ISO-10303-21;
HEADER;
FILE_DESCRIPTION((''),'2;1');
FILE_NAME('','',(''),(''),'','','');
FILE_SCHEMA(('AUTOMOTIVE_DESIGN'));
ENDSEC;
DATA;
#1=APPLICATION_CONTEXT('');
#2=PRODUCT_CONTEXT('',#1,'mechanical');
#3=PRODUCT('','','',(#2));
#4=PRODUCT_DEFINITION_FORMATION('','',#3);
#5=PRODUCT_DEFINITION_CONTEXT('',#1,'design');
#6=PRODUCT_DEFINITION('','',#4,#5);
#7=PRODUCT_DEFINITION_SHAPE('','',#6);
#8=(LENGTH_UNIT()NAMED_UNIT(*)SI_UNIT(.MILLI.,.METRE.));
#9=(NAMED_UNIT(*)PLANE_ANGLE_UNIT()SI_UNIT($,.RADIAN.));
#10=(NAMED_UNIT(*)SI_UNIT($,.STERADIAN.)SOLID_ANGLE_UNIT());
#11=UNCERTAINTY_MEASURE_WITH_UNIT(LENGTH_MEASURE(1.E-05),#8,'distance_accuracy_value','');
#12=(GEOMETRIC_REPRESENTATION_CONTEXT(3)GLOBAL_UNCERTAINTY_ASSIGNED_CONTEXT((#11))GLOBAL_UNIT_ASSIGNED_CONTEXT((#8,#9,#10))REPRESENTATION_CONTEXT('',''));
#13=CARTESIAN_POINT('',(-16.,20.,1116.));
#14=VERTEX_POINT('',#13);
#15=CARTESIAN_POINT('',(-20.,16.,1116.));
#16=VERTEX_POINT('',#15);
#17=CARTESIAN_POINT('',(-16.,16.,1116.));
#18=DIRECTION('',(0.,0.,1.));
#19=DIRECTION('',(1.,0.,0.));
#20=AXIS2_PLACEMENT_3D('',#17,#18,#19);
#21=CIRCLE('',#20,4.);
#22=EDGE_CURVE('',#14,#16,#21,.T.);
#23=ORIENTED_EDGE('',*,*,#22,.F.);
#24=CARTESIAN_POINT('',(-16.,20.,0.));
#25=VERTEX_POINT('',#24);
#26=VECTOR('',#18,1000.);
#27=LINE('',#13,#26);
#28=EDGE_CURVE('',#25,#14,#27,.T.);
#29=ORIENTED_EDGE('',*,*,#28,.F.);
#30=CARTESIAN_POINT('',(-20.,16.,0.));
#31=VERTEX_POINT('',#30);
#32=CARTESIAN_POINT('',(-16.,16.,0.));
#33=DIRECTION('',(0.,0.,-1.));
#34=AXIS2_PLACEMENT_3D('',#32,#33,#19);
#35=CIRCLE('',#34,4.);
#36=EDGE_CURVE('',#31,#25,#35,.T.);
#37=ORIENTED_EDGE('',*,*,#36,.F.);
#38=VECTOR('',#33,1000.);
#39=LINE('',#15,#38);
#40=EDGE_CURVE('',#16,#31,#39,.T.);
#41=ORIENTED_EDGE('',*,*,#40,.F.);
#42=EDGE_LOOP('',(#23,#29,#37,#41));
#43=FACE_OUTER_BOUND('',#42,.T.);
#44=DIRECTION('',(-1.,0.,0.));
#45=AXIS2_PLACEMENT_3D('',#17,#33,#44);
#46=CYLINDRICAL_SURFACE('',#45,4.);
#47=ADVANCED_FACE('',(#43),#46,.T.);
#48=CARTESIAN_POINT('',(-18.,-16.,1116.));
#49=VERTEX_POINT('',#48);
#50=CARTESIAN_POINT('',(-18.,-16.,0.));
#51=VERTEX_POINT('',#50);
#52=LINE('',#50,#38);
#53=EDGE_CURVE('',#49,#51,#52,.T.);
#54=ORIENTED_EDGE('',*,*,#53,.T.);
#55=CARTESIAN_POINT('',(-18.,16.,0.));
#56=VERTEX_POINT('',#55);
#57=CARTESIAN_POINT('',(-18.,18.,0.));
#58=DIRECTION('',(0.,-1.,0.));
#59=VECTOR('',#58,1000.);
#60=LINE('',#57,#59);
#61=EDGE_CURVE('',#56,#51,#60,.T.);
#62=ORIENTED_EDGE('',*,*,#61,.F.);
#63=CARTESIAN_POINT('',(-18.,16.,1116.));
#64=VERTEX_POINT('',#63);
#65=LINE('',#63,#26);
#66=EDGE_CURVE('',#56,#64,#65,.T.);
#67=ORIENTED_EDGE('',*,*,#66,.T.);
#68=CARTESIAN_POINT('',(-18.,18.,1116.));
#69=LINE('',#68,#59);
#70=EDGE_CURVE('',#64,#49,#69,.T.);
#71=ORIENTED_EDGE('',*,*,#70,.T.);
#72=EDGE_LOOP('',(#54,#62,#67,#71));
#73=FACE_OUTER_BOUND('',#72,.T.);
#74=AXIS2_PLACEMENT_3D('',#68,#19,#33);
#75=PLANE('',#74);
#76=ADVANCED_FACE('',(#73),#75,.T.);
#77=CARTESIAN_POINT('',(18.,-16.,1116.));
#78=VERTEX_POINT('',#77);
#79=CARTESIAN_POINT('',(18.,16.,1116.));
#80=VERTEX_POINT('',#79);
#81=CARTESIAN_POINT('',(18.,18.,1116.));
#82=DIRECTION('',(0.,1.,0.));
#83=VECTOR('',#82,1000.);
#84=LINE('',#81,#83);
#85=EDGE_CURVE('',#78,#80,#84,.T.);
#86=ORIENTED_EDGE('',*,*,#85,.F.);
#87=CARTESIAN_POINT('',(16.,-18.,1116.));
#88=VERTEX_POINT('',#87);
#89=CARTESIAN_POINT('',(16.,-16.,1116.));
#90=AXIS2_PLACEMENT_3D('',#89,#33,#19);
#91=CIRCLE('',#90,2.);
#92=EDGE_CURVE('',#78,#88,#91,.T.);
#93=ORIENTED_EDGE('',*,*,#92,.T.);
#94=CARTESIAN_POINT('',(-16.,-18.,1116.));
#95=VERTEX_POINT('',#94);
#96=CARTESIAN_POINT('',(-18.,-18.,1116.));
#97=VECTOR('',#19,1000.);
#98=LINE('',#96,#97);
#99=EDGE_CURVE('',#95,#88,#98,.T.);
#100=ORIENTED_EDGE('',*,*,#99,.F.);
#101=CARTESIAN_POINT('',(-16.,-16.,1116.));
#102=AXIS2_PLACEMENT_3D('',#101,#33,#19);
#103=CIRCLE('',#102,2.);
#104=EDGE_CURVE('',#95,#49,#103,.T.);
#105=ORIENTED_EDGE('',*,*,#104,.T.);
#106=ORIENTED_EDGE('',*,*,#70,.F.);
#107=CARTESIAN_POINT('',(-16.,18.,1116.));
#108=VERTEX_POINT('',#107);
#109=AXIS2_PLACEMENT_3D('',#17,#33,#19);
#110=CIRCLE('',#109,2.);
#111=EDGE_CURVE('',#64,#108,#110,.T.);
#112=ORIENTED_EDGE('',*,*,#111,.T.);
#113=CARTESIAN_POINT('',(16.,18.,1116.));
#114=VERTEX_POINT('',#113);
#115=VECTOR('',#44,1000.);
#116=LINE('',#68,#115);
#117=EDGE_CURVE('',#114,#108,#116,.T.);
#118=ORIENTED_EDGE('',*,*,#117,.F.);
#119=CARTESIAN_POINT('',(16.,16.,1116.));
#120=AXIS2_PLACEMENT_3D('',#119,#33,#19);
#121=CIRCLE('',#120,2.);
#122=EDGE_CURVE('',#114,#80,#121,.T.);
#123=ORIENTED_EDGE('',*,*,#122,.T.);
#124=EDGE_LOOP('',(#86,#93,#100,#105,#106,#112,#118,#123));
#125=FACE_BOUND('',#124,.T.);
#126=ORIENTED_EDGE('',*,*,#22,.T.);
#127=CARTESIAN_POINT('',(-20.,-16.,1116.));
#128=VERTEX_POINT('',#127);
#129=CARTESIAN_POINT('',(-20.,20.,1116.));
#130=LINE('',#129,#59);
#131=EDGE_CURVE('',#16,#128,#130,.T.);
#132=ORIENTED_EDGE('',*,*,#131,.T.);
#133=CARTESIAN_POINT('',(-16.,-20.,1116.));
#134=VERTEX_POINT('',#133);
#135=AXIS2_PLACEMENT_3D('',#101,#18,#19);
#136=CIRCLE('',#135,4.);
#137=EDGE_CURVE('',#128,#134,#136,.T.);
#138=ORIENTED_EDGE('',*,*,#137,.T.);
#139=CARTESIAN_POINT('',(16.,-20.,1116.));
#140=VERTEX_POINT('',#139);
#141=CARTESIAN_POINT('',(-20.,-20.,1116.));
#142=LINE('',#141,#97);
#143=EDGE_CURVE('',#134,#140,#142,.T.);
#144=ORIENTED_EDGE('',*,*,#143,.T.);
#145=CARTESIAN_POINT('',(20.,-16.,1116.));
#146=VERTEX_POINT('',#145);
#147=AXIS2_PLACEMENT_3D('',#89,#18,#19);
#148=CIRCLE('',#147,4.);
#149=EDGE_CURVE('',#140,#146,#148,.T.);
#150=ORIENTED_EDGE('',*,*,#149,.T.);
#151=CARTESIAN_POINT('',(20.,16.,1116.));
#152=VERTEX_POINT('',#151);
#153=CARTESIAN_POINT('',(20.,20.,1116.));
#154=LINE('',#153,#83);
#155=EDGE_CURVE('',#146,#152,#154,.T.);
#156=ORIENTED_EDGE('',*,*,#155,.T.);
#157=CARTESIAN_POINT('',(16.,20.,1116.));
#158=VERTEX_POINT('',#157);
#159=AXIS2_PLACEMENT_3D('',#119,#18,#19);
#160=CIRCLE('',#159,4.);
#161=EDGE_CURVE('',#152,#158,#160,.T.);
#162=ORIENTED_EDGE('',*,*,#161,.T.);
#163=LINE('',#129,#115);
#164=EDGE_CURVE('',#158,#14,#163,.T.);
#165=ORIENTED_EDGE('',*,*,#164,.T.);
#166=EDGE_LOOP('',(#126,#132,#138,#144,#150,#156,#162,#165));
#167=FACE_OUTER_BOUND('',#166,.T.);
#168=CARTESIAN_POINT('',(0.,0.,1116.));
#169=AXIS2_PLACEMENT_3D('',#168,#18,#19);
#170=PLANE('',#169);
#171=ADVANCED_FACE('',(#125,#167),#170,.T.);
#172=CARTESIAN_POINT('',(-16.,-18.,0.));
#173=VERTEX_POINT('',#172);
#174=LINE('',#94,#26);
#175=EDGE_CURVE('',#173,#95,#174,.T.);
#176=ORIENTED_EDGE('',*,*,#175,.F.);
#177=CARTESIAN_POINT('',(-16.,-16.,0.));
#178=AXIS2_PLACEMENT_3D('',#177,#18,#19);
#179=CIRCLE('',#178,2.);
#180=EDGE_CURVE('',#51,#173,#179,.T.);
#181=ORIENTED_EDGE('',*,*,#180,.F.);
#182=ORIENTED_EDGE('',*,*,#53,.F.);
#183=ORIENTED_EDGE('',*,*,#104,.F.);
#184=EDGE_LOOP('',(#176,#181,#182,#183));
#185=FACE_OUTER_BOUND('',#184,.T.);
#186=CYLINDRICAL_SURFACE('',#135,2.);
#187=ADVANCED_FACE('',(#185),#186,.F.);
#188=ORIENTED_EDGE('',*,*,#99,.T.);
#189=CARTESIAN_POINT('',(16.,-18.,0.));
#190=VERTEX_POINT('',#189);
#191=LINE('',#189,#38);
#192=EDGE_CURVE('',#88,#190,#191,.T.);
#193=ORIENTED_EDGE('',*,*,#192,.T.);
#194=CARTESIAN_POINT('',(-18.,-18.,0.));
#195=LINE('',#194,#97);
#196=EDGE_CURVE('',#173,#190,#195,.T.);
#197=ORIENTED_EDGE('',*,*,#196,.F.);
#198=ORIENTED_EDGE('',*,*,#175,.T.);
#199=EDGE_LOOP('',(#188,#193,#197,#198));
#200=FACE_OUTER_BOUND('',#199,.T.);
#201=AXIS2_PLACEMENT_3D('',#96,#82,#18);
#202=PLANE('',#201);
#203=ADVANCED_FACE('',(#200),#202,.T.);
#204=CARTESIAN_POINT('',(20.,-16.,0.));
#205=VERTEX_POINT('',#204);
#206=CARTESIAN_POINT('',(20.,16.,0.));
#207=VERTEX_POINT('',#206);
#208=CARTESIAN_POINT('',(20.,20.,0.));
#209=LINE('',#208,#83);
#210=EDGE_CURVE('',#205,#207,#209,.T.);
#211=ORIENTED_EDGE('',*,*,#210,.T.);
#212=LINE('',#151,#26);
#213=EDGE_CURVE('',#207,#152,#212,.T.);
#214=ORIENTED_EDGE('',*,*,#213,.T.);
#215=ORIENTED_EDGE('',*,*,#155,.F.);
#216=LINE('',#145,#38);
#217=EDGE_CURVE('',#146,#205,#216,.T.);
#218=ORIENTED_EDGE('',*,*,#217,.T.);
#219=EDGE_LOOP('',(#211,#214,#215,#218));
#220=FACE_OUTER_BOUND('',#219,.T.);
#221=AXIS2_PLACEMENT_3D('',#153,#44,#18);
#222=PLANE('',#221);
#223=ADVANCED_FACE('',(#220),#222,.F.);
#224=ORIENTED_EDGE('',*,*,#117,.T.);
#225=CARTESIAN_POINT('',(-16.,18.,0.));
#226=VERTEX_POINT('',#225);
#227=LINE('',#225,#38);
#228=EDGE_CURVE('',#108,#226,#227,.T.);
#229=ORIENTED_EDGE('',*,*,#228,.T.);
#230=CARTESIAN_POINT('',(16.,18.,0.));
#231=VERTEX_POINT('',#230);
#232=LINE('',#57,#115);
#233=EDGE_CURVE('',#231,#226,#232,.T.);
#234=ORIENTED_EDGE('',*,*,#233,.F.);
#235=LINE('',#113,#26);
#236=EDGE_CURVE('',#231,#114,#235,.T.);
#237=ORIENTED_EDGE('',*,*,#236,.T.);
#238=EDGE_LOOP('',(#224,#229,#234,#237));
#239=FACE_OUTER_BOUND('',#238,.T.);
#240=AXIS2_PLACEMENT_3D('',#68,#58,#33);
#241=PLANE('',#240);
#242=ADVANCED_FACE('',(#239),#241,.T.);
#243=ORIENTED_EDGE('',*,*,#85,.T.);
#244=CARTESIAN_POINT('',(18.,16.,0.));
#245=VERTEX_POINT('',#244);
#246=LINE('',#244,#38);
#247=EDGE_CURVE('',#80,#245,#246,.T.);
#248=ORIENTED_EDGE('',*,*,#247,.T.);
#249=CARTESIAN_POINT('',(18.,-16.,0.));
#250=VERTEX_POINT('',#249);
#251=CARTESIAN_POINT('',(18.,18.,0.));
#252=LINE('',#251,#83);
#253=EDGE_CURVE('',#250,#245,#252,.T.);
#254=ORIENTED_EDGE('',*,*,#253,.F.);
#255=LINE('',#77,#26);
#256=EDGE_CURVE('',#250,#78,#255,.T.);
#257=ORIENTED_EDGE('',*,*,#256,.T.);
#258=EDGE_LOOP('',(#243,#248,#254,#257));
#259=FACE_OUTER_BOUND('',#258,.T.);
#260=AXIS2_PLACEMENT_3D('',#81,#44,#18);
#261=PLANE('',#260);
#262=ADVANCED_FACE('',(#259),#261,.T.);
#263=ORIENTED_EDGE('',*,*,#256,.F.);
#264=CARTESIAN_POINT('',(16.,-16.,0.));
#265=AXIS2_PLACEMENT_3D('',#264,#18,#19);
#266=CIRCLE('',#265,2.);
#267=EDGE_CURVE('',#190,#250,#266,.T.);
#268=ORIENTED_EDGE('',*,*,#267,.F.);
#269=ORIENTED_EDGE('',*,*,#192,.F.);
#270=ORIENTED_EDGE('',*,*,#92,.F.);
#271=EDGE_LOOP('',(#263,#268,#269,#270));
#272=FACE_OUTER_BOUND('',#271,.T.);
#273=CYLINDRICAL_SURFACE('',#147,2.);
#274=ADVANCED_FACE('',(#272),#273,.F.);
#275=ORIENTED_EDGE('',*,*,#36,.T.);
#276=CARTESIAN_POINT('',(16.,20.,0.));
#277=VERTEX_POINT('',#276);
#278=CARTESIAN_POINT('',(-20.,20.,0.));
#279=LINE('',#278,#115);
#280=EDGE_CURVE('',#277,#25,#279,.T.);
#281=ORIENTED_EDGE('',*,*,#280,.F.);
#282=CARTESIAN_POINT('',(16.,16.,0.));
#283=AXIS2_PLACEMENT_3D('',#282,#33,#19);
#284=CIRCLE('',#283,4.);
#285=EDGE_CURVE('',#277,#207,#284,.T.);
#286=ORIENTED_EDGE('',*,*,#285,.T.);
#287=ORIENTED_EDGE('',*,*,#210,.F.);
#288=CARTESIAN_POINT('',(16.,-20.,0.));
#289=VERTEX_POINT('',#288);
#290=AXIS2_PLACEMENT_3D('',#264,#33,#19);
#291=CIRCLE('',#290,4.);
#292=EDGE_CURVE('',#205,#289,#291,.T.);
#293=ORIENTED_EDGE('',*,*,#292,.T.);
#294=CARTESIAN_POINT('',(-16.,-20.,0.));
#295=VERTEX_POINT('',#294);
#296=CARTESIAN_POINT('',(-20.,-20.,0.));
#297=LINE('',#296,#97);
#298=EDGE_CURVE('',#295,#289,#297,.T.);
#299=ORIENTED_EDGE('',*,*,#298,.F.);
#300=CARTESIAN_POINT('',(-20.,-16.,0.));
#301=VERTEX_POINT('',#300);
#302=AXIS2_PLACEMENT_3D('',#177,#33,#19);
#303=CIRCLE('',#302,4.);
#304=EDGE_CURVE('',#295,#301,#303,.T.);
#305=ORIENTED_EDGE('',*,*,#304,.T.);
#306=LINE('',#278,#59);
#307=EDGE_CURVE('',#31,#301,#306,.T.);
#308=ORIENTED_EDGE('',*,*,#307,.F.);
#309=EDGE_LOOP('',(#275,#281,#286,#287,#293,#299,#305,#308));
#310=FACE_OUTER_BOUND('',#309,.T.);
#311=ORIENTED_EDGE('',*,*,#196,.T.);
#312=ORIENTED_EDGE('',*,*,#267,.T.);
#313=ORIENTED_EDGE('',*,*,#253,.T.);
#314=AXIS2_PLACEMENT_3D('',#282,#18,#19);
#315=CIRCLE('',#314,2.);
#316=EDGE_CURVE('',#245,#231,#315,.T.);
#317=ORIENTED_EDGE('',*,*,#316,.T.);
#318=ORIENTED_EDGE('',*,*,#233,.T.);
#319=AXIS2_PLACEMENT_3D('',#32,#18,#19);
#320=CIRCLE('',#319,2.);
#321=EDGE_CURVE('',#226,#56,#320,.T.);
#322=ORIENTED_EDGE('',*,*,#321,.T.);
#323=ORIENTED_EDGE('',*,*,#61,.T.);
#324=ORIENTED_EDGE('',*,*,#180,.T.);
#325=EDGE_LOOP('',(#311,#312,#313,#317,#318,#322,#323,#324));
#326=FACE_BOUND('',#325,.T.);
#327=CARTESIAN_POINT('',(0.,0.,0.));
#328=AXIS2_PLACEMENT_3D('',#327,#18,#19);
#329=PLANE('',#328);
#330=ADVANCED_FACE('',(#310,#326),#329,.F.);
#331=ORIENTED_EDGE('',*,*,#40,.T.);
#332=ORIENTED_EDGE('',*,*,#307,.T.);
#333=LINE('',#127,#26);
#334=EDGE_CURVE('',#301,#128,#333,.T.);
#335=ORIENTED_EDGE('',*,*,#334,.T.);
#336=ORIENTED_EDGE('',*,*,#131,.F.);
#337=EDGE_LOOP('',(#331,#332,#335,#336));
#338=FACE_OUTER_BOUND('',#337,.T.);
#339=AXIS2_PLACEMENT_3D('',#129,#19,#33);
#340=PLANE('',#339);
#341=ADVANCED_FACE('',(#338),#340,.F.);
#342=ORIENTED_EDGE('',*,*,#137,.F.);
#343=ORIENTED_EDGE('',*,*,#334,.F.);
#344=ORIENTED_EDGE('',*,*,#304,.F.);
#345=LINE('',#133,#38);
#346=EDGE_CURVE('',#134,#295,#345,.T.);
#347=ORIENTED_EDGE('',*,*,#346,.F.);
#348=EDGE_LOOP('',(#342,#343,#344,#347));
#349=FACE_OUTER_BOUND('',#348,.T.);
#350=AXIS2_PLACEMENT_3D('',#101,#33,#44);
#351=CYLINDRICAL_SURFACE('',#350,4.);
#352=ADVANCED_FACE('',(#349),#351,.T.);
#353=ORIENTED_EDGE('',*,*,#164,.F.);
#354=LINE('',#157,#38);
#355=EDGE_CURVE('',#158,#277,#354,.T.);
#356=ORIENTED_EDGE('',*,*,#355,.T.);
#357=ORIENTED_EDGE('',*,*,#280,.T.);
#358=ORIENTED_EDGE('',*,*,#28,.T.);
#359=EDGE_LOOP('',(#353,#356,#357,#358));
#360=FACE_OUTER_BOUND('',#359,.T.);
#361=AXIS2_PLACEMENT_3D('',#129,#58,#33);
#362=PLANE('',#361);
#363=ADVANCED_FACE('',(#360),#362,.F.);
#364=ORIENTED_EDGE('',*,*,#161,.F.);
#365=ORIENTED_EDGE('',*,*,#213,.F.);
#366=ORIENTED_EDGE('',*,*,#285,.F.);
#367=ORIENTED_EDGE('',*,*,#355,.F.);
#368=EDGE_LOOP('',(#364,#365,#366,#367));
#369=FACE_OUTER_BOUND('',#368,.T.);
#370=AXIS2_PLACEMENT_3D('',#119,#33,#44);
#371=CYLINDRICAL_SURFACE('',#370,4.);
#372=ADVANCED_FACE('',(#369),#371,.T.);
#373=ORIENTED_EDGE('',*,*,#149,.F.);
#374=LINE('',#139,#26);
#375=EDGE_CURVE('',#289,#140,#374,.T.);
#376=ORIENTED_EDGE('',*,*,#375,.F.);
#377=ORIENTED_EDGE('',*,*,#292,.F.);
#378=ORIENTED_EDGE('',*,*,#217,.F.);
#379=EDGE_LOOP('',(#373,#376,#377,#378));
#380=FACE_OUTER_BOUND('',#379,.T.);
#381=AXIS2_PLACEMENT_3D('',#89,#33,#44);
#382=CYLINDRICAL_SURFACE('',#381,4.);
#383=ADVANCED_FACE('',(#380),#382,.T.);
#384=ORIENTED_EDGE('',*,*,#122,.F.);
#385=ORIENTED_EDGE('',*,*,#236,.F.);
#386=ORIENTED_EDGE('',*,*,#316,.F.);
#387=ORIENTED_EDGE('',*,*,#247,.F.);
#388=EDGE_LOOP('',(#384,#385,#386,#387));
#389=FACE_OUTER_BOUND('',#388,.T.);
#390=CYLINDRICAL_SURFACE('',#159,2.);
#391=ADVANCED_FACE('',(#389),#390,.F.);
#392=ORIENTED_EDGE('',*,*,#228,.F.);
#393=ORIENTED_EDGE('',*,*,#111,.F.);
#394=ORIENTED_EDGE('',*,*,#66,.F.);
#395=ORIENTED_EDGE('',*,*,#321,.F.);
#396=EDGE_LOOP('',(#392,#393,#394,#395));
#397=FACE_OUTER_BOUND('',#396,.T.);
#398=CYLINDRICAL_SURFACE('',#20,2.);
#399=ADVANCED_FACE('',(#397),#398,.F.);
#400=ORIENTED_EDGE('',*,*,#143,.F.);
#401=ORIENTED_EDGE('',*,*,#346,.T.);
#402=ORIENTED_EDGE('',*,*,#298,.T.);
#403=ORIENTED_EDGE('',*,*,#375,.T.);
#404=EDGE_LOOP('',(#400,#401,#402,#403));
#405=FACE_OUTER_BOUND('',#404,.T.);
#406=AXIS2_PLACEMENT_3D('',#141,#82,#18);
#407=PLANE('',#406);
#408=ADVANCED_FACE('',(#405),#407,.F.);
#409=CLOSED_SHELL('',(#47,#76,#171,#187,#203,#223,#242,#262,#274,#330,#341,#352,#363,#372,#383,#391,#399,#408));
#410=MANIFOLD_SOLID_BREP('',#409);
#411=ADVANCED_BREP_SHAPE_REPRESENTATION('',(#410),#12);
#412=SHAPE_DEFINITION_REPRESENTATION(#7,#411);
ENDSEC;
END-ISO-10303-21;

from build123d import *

# Parameters (mm, degrees)
SKETCH1_W           = 40
SKETCH1_H           = 40
SKETCH1_W_2         = 36
SKETCH1_H_2         = 36
BOSS_EXTRUDE1_DEPTH = 1116
FILLET1_R           = 2
FILLET2_R           = 4


with BuildPart() as part:
    # Sketch1 → Boss-Extrude1 (new body)
    with BuildSketch(Plane.XY):
        Rectangle(SKETCH1_W, SKETCH1_H)
        Rectangle(SKETCH1_W_2, SKETCH1_H_2, mode=Mode.SUBTRACT)
    extrude(amount=BOSS_EXTRUDE1_DEPTH)

    # Fillet1
    fillet1_edges = [part.edges().sort_by_distance(p)[0] for p in [
        (18, -18, 558),
        (18, 18, 558),
        (-18, 18, 558),
        (-18, -18, 558),
    ]]
    fillet(fillet1_edges, radius=FILLET1_R)

    # Fillet2
    fillet2_edges = [part.edges().sort_by_distance(p)[0] for p in [
        (20, -20, 558),
        (-20, -20, 558),
        (-20, 20, 558),
        (20, 20, 558),
    ]]
    fillet(fillet2_edges, radius=FILLET2_R)


solid = part.part
